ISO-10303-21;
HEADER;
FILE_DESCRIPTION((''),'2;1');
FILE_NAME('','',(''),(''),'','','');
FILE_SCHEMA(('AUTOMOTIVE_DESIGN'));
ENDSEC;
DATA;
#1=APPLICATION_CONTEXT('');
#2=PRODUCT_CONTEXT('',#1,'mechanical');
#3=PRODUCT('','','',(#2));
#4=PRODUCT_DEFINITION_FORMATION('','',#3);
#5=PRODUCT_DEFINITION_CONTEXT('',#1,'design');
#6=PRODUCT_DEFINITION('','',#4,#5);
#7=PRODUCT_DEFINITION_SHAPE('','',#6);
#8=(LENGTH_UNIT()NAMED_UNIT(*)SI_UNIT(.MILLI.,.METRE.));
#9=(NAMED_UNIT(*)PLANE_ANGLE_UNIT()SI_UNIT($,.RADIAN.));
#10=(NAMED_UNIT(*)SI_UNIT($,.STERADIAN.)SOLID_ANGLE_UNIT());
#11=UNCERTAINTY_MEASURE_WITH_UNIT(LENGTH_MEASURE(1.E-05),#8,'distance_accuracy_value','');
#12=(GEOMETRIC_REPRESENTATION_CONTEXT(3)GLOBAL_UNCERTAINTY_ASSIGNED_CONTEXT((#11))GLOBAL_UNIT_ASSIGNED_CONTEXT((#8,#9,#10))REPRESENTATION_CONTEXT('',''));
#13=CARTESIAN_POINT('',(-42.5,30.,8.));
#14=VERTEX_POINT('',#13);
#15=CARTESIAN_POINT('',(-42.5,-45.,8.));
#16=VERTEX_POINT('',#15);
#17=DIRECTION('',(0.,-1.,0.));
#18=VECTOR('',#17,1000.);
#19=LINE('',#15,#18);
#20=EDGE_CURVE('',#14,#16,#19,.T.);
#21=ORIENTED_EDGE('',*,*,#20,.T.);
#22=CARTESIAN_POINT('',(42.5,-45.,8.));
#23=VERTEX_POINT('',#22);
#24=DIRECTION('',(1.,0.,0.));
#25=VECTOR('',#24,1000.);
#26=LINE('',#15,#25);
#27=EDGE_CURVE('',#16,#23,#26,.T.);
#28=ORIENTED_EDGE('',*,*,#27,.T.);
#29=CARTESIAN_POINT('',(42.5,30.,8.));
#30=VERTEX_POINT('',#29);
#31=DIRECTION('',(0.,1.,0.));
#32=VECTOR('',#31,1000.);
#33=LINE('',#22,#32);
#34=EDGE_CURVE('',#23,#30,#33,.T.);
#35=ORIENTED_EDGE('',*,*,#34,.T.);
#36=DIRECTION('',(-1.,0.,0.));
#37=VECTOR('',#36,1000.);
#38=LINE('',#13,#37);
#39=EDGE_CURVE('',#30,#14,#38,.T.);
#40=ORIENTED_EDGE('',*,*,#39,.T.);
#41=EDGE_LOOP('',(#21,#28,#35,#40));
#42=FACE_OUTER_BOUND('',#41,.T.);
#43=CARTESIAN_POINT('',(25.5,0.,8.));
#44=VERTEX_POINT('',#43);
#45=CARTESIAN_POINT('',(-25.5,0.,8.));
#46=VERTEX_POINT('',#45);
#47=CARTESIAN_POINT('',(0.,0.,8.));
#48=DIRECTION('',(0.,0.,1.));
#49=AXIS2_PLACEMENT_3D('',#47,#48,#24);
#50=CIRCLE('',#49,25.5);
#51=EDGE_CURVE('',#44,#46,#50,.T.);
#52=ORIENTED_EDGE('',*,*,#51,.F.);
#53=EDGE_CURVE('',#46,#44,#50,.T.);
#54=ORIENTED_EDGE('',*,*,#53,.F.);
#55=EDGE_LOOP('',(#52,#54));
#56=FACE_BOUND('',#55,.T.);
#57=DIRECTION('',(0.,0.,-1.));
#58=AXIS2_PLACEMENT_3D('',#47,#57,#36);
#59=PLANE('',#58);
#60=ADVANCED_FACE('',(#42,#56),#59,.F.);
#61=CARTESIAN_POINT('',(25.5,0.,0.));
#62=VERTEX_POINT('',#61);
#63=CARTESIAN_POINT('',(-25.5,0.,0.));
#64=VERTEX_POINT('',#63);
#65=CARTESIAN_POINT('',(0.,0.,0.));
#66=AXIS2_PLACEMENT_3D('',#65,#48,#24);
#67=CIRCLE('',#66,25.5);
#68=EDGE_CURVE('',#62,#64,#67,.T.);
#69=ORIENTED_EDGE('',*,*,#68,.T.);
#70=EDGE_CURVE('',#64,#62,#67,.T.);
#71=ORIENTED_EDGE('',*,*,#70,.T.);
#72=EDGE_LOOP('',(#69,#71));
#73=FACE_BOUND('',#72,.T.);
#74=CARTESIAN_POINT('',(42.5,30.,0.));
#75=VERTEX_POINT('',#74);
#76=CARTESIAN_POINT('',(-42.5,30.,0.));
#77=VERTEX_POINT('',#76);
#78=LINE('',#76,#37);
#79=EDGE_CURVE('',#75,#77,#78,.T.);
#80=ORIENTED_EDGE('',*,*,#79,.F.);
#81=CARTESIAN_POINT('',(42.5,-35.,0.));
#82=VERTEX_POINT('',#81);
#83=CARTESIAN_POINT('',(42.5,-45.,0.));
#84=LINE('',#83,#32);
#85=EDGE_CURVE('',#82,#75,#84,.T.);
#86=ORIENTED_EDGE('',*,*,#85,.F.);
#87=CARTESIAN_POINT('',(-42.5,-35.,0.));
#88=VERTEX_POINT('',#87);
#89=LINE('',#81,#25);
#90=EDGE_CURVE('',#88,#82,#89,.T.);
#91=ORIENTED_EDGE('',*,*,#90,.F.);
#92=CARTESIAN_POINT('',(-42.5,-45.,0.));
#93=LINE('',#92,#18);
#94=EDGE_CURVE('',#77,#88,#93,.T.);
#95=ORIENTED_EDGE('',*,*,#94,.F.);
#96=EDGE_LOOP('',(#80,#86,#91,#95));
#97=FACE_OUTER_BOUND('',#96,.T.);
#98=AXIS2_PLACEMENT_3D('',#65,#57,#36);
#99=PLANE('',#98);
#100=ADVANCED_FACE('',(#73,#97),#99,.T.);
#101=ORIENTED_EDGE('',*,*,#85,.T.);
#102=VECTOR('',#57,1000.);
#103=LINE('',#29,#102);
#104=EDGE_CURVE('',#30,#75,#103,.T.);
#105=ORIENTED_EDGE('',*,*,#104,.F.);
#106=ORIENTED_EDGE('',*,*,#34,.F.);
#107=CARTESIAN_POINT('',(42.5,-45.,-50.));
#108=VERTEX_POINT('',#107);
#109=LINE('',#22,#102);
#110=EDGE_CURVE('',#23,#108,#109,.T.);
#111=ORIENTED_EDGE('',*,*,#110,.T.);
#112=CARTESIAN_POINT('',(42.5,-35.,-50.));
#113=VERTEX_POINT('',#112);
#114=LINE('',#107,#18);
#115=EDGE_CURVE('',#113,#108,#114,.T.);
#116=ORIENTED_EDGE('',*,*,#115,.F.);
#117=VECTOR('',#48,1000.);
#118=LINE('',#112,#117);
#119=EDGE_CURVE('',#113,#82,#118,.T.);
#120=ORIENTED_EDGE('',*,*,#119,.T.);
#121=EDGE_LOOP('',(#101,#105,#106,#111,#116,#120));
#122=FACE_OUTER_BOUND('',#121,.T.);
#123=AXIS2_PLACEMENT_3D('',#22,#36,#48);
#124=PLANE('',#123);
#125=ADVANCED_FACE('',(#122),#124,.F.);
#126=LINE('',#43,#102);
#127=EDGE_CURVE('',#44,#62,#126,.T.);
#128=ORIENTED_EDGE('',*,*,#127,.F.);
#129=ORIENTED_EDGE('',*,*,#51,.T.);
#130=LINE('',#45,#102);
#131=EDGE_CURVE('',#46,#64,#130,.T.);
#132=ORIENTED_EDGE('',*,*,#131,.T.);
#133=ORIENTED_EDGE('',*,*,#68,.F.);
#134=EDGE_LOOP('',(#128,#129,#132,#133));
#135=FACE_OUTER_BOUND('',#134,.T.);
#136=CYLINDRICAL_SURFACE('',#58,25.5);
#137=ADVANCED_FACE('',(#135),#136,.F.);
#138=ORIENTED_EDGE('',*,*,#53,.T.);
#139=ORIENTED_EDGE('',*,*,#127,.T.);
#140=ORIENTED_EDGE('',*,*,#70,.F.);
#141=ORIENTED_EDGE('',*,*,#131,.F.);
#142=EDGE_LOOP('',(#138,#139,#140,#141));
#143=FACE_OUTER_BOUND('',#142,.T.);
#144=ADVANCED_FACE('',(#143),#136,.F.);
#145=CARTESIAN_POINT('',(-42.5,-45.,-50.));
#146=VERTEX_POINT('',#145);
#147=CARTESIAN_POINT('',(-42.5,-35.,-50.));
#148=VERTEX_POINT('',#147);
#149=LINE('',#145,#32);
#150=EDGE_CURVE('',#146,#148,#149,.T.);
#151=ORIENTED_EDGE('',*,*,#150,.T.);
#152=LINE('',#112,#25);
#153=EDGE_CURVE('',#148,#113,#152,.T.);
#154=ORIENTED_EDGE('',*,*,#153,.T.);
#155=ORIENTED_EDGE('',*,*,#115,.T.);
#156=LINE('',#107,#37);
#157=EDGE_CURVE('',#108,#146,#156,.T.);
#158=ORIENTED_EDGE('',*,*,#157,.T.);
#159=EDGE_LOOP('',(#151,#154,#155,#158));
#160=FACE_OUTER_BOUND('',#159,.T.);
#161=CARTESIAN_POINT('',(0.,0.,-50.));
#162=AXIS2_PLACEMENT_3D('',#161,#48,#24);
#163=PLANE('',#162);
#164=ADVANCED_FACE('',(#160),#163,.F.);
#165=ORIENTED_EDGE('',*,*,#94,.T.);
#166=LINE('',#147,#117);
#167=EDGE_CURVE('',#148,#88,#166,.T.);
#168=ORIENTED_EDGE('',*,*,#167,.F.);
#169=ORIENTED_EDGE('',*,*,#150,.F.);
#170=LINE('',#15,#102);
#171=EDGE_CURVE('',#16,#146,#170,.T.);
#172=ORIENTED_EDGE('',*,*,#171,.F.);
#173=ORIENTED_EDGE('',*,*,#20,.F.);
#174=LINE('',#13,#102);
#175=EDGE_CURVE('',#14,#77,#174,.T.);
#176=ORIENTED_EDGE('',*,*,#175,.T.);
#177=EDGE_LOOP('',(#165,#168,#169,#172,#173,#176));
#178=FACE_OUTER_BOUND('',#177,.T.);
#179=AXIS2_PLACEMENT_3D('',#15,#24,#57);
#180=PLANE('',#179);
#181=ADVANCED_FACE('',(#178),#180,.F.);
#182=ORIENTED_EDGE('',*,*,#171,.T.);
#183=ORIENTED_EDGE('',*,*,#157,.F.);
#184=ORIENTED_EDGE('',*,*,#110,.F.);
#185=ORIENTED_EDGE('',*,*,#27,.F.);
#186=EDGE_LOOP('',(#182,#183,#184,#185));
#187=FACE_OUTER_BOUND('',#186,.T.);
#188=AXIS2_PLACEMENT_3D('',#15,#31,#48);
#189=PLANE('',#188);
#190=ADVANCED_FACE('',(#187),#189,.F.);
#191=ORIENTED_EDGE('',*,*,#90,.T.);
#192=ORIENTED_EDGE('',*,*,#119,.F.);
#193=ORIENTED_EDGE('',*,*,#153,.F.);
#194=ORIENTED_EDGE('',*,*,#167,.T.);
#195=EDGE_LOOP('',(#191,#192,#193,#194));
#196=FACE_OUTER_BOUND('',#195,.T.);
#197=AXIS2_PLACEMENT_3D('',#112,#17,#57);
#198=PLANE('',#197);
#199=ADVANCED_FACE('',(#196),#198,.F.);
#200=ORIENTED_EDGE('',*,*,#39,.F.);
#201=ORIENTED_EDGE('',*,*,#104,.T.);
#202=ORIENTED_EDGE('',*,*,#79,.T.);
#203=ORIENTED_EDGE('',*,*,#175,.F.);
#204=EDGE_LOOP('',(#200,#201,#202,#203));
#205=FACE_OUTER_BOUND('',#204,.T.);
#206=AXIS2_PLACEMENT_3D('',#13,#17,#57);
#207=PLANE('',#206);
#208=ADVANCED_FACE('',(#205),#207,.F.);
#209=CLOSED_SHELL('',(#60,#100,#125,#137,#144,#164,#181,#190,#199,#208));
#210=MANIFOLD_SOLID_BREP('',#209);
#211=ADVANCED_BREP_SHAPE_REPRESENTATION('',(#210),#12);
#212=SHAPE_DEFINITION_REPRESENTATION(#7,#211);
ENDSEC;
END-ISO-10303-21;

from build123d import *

# Parameters (mm, degrees)
SKETCH_1_W      = 85
SKETCH_1_H      = 75
SKETCH_1_R      = 25.5
EXTRUDE_1_DEPTH = 8
SKETCH_2_W      = 85
SKETCH_2_H      = 10
EXTRUDE_2_DEPTH = 50


with BuildPart() as part:
    # 草图1 → 凸台-拉伸1 (new body)
    with BuildSketch(Plane.XY):
        with Locations((0, -7.5)):
            Rectangle(SKETCH_1_W, SKETCH_1_H)
        Circle(SKETCH_1_R, mode=Mode.SUBTRACT)
    extrude(amount=EXTRUDE_1_DEPTH)

    # 草图2 → 凸台-拉伸2 (add)
    with BuildSketch(Plane(origin=(0, 0, 0), x_dir=(-1, 0, 0), z_dir=(0, 0, -1))):
        with Locations((0, -40)):
            Rectangle(SKETCH_2_W, SKETCH_2_H)
    extrude(amount=EXTRUDE_2_DEPTH)


solid = part.part
